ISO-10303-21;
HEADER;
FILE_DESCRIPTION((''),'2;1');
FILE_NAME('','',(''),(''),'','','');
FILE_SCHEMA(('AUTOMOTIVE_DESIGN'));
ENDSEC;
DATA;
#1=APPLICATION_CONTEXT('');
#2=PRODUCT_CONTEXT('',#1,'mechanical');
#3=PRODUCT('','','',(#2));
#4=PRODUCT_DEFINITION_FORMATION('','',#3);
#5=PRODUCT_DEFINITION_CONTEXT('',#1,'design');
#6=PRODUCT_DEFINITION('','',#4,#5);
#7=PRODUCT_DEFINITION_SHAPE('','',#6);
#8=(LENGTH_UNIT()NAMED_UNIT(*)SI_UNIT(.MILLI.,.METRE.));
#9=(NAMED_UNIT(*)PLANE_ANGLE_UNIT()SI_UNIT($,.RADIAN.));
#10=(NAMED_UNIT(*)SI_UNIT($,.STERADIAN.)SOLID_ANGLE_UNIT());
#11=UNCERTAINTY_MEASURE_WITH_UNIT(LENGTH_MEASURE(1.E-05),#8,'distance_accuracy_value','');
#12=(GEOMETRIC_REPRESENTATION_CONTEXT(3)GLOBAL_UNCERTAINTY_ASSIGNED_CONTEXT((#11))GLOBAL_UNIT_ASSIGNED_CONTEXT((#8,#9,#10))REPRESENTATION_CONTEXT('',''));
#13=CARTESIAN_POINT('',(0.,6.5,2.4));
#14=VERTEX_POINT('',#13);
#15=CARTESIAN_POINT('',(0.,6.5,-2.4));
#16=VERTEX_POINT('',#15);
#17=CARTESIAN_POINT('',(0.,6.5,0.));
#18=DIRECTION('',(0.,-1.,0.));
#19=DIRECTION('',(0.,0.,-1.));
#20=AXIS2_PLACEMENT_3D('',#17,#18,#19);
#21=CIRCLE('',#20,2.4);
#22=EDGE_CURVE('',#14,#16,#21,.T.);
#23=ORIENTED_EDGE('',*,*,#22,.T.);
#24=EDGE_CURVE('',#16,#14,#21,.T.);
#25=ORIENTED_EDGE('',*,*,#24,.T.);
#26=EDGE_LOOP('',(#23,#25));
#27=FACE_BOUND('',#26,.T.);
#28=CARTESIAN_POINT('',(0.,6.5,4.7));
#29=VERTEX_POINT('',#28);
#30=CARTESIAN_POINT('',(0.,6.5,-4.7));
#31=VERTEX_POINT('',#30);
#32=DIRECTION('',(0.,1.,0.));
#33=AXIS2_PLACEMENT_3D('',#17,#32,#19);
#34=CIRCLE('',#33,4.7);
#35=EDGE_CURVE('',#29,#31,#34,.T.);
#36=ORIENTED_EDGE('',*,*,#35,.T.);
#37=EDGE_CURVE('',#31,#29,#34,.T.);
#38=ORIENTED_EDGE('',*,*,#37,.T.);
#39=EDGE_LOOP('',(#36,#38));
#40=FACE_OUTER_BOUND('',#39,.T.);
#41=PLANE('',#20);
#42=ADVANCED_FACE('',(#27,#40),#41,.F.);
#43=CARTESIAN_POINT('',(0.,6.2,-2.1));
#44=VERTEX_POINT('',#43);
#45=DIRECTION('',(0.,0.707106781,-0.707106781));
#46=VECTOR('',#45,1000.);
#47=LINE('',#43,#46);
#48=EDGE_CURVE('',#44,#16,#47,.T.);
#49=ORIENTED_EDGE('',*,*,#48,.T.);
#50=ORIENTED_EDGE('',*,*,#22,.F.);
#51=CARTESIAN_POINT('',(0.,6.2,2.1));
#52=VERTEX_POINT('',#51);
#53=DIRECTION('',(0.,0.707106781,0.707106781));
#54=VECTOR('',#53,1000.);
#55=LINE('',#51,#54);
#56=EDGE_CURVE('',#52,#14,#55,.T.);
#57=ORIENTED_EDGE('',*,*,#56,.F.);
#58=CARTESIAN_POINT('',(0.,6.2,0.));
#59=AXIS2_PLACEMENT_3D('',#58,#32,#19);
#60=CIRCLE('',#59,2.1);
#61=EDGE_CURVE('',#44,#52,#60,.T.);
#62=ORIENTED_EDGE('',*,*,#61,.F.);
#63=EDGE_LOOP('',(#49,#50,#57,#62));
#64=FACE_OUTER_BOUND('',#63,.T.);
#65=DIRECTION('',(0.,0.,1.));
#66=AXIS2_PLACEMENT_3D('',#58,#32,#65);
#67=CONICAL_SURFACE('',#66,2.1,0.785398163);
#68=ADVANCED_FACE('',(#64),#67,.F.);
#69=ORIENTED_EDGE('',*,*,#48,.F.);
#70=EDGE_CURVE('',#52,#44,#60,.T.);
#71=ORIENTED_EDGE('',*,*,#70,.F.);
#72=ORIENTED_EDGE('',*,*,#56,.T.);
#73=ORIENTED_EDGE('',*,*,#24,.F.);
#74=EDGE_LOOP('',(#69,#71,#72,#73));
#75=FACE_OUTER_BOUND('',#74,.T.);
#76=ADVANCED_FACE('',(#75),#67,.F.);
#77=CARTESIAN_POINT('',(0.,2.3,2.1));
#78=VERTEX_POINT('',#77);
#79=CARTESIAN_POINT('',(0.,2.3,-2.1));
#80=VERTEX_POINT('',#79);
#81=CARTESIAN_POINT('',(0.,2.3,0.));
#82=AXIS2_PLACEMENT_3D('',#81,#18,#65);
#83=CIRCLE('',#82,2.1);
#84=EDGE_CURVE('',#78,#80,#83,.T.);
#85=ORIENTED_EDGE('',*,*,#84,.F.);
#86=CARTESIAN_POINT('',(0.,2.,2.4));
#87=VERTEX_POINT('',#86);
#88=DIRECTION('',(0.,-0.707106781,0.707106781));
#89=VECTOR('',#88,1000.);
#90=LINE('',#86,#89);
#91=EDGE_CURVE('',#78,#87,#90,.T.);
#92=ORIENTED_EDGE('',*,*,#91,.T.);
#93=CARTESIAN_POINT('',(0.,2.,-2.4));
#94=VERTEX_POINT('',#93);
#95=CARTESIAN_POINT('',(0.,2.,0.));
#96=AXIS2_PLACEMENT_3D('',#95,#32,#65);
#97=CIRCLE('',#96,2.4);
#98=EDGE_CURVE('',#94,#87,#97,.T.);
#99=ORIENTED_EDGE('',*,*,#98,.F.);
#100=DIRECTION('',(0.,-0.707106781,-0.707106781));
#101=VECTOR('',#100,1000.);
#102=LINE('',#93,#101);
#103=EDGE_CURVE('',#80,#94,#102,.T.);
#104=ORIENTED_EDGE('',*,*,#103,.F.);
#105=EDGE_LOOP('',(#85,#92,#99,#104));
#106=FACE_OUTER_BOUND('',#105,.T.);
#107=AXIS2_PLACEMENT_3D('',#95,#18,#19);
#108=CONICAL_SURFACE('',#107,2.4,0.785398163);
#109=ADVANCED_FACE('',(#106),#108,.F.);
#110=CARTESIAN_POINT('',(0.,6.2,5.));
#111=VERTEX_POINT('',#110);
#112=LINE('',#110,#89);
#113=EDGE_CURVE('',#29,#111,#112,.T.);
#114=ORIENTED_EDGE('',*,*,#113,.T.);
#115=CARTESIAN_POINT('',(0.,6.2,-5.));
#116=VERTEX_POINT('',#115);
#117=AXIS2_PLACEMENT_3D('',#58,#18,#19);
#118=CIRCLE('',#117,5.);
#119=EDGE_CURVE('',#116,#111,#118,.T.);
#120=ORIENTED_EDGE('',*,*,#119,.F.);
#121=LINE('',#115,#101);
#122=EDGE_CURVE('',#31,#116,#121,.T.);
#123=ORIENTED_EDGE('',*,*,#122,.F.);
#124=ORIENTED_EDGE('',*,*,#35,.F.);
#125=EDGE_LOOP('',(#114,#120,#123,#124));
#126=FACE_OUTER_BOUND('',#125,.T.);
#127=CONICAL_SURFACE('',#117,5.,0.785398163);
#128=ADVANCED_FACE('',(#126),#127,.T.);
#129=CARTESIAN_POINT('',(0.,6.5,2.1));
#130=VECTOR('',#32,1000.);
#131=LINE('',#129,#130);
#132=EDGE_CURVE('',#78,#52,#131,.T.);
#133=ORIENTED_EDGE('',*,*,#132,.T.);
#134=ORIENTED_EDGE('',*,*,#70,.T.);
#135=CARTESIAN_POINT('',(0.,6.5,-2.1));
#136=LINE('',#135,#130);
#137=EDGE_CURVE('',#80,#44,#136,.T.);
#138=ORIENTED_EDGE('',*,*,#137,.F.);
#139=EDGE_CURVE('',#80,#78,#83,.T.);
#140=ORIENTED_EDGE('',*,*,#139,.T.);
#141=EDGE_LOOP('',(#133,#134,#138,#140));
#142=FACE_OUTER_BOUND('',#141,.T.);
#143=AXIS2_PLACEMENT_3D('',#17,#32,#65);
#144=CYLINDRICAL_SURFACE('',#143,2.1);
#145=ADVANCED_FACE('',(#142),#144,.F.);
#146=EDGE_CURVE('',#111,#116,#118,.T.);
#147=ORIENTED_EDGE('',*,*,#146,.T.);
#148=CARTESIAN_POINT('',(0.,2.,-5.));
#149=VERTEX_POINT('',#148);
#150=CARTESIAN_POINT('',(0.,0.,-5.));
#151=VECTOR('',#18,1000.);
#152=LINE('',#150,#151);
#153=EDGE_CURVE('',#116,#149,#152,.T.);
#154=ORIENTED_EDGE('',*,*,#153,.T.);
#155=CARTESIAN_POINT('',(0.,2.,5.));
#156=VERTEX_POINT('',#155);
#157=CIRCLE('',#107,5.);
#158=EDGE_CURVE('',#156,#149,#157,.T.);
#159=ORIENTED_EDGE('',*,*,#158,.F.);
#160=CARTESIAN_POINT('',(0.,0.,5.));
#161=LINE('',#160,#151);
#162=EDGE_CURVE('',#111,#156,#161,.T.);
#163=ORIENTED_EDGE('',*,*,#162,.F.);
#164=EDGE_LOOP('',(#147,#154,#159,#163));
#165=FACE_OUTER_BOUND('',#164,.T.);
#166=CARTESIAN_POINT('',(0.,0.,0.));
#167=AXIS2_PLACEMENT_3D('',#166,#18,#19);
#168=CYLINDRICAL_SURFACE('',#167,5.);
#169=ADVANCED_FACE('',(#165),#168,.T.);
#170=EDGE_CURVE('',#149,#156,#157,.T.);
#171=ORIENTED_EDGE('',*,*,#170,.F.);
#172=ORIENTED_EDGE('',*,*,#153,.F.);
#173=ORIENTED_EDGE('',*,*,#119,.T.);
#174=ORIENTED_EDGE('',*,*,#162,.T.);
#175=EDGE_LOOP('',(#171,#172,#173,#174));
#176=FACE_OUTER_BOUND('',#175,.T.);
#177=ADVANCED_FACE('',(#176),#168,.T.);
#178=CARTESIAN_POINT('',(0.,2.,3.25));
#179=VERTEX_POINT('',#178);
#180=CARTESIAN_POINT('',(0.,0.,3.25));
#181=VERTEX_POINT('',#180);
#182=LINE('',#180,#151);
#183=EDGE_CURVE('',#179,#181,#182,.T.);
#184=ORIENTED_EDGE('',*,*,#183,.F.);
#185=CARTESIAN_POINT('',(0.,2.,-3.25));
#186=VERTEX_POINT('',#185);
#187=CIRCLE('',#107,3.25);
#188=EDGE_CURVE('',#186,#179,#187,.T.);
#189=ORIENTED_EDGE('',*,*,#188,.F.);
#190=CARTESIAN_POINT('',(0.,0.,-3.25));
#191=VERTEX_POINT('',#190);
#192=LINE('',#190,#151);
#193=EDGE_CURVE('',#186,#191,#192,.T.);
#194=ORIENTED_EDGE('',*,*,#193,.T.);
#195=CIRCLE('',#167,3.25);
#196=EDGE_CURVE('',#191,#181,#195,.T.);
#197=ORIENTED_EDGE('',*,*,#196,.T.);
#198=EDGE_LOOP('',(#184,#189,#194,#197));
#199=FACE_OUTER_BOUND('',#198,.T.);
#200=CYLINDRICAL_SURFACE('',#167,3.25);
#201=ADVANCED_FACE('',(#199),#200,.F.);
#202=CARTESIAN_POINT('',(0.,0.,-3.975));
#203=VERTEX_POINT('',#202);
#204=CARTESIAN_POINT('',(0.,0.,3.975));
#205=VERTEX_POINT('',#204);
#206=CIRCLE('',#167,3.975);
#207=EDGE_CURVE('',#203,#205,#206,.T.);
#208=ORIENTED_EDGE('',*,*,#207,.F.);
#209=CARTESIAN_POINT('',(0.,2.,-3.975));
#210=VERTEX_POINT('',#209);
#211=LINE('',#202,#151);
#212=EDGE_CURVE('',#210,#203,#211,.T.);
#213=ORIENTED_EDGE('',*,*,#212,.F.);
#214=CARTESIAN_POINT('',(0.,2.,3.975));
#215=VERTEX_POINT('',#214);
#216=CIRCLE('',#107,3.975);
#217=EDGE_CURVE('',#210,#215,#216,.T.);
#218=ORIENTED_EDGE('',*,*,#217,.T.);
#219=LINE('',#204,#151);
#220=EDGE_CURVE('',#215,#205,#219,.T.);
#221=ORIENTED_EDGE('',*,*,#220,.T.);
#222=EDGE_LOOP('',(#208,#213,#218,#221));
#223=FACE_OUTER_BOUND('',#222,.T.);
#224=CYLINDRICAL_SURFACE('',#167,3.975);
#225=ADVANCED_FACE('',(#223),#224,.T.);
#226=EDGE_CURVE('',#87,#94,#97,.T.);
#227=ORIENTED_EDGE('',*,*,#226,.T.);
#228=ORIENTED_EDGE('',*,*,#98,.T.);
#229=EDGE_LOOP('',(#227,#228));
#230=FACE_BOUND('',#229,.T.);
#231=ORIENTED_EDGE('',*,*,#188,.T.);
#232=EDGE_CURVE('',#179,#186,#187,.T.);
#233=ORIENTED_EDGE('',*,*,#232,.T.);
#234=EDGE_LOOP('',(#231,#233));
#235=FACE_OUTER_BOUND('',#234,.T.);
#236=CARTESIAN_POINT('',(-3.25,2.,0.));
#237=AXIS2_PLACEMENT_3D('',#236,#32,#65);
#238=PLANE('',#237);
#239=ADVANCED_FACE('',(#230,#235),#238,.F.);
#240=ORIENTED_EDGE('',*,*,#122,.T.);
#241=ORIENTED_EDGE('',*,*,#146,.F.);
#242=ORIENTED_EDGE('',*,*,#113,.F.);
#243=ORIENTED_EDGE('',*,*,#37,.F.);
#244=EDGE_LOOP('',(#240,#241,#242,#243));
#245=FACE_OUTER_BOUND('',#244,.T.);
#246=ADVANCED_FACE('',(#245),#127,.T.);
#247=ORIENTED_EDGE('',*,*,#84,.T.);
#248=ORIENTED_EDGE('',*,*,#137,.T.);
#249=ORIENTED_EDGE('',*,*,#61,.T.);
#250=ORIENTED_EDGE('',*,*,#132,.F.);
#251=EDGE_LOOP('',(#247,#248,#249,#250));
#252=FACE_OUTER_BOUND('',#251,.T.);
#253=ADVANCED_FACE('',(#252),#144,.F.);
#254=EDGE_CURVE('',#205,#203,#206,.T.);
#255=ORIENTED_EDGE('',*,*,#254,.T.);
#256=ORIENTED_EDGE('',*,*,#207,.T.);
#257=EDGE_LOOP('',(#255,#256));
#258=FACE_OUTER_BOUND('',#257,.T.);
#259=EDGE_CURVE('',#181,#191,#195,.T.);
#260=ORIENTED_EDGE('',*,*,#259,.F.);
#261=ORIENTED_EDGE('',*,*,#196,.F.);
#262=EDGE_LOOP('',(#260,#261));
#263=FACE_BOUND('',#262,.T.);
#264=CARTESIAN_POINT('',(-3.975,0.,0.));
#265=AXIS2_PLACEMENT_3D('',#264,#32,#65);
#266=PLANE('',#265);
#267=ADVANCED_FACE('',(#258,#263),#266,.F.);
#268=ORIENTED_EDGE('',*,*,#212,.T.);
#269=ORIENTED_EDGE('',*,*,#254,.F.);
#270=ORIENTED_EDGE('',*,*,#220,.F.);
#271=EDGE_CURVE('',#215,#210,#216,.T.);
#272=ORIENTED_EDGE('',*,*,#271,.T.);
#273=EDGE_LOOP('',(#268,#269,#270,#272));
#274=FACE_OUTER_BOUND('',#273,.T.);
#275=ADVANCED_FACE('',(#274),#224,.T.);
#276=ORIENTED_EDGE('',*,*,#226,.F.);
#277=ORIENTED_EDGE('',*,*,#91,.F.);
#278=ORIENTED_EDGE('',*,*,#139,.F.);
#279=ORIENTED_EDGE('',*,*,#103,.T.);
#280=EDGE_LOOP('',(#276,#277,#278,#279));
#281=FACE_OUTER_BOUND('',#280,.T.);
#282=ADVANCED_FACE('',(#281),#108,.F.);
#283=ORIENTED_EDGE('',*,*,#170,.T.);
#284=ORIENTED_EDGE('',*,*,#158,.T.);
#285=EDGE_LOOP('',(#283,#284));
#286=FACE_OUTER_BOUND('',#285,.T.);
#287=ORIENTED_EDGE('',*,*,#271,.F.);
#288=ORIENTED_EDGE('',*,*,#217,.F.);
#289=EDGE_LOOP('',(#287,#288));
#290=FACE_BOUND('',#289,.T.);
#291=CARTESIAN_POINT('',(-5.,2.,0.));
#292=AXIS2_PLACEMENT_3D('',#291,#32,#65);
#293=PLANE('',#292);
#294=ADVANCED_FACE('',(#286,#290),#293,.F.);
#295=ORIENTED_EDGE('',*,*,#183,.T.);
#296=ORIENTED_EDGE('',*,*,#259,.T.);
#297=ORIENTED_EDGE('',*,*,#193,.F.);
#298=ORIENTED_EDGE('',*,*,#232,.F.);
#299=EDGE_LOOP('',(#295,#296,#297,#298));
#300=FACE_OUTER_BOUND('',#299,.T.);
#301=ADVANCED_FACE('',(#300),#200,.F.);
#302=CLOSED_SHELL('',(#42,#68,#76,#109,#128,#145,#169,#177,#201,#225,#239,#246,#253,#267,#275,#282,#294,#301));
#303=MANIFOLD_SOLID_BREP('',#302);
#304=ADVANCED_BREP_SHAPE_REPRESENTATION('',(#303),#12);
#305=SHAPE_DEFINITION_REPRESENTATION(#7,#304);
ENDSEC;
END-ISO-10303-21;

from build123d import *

# Parameters (mm, degrees)
HOLE_WIZARD_M5_1_D = 4.2
CHAMFER_1_SIZE     = 0.3


with BuildPart() as part:
    # 草图1 → 旋转1 (revolve)
    with BuildSketch(Plane.XY, mode=Mode.PRIVATE) as revolve_1_sk:
        Polygon((0, 6.5), (-5, 6.5), (-5, 2), (-3.975, 2), (-3.975, 0), (-3.25, 0), (-3.25, 2), (0, 2), align=None)
    revolve(revolve_1_sk.sketch.rotate(Axis((0, 0, 0), (0, 1, 0)), 270), axis=Axis((0, 0, 0), (0, 1, 0)))

    # M5 螺纹孔1 (through all)
    with Locations(Plane(origin=(0, 6.5, 0), x_dir=(1, 0, 0), z_dir=(0, 1, 0))):
        with Locations((0, 0)):
            Hole(HOLE_WIZARD_M5_1_D / 2)

    # 倒角1
    chamfer_1_edges = [part.edges().sort_by_distance(p)[0] for p in [
        (2.1, 2, 0),
        (2.1, 6.5, 0),
        (0, 6.5, 5),
    ]]
    chamfer(chamfer_1_edges, length=CHAMFER_1_SIZE)


solid = part.part
